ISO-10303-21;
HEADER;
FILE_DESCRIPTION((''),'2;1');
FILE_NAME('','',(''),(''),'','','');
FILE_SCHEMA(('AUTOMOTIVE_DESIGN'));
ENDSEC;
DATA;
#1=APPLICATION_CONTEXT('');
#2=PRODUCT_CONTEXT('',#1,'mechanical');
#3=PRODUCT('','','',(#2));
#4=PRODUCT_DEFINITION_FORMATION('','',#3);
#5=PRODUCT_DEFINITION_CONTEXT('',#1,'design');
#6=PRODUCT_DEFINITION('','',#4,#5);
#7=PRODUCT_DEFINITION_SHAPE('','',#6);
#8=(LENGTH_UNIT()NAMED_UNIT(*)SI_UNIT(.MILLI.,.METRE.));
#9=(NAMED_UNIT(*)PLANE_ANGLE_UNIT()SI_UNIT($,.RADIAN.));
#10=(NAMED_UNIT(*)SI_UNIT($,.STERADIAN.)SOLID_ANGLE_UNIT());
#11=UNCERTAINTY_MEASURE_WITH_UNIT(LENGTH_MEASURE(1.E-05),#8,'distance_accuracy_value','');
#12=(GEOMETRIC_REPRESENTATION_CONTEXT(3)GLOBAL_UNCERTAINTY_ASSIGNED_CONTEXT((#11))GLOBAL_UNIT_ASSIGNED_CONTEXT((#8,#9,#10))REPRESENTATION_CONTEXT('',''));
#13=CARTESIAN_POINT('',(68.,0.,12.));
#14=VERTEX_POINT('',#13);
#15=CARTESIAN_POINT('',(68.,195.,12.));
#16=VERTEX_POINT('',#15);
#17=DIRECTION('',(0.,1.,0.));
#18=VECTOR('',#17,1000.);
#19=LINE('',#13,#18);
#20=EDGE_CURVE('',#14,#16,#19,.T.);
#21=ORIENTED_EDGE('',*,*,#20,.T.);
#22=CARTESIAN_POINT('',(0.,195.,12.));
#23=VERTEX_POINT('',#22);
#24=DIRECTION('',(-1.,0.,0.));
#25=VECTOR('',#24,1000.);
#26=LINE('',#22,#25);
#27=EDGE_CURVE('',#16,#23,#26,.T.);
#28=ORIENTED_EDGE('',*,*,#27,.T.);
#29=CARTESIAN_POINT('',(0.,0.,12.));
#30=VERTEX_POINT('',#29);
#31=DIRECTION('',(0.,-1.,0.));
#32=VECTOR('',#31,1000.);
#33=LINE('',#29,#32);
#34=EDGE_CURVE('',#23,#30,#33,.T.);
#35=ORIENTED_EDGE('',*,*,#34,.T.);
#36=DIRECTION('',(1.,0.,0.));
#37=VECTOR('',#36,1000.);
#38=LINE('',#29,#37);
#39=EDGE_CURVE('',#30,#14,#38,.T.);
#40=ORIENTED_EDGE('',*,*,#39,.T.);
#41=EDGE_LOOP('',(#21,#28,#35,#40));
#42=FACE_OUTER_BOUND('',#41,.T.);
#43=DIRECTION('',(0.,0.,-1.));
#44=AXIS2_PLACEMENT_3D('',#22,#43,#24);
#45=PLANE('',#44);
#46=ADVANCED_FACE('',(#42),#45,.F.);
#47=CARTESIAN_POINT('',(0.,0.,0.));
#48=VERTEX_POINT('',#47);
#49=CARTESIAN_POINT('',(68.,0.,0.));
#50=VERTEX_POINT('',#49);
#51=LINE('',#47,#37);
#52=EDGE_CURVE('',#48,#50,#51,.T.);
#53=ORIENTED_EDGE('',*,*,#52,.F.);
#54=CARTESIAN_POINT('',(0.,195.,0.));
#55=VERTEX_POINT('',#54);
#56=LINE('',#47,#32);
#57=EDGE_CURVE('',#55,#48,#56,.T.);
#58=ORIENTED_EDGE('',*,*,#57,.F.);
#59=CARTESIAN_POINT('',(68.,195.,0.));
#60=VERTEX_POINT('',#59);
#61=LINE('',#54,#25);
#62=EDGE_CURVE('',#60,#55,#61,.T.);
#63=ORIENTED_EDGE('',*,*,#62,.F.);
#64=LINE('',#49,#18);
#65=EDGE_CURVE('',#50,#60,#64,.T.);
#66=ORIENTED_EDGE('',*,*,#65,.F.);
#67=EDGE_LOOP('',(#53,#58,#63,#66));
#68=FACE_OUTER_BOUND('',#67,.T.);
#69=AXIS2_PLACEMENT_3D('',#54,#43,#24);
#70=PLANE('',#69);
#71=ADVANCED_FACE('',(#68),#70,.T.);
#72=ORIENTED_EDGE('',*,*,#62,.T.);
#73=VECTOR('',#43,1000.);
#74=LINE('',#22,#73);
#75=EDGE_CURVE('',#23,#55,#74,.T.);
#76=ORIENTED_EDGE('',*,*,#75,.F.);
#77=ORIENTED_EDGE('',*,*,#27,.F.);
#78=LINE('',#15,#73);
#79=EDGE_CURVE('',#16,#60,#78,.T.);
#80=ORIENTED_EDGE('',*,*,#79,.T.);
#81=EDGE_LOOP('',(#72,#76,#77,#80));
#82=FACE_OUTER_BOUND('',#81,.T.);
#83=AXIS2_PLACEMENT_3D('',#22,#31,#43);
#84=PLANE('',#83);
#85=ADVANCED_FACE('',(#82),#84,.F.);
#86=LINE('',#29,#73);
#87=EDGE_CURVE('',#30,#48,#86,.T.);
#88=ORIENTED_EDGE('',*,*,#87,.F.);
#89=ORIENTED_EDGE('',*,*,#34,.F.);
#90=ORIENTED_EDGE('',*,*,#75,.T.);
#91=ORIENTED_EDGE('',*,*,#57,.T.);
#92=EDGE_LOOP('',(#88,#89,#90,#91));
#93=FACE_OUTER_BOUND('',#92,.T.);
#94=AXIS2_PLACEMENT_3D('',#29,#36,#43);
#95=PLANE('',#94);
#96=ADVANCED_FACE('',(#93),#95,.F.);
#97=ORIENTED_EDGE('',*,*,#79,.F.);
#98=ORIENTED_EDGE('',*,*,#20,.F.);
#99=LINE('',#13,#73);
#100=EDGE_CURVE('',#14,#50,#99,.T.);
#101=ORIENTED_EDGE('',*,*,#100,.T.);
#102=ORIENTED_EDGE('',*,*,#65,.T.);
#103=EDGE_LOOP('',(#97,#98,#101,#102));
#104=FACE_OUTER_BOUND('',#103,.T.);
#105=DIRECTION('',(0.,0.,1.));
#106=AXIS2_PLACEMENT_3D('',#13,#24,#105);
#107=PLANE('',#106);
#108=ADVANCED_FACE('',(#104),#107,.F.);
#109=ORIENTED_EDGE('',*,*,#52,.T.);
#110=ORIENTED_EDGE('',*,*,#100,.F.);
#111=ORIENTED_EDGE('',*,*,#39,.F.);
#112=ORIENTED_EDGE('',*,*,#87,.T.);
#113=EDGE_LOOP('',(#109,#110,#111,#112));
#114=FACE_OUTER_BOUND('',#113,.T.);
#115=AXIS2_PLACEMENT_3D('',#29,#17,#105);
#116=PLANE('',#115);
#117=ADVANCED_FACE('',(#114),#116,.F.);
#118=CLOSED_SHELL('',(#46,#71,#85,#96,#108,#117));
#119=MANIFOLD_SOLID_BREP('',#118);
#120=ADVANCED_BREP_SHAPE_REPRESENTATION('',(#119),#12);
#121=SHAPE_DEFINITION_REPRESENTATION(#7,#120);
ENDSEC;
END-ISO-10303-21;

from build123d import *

# Parameters (mm, degrees)
SKETCH1_W           = 68
SKETCH1_H           = 195
BOSS_EXTRUDE1_DEPTH = 12


with BuildPart() as part:
    # Sketch1 → Boss-Extrude1 (new body)
    with BuildSketch(Plane.XY):
        with Locations((34, 97.5)):
            Rectangle(SKETCH1_W, SKETCH1_H)
    extrude(amount=BOSS_EXTRUDE1_DEPTH)


solid = part.part
